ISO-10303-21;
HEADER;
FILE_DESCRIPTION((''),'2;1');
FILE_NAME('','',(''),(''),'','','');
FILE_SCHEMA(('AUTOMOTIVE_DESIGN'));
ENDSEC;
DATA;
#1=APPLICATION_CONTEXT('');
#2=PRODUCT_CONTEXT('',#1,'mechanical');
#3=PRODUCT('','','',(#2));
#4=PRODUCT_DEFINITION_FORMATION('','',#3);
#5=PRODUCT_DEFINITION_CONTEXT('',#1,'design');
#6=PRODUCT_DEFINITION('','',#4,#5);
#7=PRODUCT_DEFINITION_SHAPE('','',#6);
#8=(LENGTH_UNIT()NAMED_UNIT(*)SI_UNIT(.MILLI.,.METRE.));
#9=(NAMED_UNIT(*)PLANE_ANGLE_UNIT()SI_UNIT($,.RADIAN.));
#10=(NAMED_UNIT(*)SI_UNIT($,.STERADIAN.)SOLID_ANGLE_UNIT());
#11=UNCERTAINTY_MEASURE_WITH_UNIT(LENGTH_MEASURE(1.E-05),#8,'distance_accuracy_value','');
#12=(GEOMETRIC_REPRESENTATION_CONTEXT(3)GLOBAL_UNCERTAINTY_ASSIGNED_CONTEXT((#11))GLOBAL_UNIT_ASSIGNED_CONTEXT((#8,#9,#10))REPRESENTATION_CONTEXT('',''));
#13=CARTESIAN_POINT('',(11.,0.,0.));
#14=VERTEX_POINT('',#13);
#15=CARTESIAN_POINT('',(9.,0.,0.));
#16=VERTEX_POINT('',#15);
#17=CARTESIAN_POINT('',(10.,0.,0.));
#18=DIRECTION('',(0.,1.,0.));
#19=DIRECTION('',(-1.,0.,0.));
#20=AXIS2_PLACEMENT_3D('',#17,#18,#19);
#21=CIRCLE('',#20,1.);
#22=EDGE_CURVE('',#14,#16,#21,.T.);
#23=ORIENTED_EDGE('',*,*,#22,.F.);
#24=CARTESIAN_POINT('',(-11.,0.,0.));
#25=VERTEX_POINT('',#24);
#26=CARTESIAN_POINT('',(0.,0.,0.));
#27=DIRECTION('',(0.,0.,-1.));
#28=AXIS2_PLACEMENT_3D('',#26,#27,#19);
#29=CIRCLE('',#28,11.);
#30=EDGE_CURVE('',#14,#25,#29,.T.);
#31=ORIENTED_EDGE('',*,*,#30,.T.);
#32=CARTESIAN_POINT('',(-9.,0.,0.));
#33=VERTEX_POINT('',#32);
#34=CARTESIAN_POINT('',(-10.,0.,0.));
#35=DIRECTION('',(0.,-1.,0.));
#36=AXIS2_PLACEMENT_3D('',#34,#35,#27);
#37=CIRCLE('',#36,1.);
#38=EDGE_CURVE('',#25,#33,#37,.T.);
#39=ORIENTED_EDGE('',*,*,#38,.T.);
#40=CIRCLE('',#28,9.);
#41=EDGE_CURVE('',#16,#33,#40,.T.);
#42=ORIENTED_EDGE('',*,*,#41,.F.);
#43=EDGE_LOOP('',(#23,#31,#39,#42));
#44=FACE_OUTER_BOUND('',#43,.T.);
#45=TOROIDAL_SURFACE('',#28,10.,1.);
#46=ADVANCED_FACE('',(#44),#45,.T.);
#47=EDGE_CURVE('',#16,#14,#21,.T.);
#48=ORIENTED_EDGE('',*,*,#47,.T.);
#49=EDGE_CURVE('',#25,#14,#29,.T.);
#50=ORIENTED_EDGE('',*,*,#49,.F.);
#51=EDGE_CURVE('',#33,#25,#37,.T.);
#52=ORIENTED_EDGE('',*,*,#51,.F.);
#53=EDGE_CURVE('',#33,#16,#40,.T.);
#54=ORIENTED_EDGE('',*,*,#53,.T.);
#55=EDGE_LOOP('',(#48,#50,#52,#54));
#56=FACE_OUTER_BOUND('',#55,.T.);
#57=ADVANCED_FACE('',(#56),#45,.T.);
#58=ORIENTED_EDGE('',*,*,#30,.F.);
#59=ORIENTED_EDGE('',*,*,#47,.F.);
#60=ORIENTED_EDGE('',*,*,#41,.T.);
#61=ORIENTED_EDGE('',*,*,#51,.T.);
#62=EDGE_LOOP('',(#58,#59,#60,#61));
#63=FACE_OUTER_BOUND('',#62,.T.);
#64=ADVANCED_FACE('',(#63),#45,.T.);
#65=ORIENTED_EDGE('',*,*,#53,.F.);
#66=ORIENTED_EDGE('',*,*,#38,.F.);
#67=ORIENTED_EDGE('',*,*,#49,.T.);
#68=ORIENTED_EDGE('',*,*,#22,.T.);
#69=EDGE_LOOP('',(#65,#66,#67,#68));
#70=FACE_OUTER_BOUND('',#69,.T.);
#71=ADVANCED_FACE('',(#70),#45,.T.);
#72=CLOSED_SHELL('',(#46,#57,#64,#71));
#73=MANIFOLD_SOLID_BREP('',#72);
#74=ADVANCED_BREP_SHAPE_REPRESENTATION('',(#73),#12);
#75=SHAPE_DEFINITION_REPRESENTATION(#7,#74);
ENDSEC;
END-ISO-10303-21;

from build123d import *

# Parameters (mm, degrees)
SKETCH1_R = 1


with BuildPart() as part:
    # Sketch1 → Revolve1 (revolve)
    with BuildSketch(Plane(origin=(0, 0, 0), x_dir=(1, 0, 0), z_dir=(0, 1, 0)), mode=Mode.PRIVATE) as revolve1_sk:
        with Locations((10, 0)):
            Circle(SKETCH1_R)
    revolve(revolve1_sk.sketch.rotate(Axis((0, 0, 0), (0, 0, 1)), 180), axis=Axis((0, 0, 0), (0, 0, 1)))


solid = part.part
